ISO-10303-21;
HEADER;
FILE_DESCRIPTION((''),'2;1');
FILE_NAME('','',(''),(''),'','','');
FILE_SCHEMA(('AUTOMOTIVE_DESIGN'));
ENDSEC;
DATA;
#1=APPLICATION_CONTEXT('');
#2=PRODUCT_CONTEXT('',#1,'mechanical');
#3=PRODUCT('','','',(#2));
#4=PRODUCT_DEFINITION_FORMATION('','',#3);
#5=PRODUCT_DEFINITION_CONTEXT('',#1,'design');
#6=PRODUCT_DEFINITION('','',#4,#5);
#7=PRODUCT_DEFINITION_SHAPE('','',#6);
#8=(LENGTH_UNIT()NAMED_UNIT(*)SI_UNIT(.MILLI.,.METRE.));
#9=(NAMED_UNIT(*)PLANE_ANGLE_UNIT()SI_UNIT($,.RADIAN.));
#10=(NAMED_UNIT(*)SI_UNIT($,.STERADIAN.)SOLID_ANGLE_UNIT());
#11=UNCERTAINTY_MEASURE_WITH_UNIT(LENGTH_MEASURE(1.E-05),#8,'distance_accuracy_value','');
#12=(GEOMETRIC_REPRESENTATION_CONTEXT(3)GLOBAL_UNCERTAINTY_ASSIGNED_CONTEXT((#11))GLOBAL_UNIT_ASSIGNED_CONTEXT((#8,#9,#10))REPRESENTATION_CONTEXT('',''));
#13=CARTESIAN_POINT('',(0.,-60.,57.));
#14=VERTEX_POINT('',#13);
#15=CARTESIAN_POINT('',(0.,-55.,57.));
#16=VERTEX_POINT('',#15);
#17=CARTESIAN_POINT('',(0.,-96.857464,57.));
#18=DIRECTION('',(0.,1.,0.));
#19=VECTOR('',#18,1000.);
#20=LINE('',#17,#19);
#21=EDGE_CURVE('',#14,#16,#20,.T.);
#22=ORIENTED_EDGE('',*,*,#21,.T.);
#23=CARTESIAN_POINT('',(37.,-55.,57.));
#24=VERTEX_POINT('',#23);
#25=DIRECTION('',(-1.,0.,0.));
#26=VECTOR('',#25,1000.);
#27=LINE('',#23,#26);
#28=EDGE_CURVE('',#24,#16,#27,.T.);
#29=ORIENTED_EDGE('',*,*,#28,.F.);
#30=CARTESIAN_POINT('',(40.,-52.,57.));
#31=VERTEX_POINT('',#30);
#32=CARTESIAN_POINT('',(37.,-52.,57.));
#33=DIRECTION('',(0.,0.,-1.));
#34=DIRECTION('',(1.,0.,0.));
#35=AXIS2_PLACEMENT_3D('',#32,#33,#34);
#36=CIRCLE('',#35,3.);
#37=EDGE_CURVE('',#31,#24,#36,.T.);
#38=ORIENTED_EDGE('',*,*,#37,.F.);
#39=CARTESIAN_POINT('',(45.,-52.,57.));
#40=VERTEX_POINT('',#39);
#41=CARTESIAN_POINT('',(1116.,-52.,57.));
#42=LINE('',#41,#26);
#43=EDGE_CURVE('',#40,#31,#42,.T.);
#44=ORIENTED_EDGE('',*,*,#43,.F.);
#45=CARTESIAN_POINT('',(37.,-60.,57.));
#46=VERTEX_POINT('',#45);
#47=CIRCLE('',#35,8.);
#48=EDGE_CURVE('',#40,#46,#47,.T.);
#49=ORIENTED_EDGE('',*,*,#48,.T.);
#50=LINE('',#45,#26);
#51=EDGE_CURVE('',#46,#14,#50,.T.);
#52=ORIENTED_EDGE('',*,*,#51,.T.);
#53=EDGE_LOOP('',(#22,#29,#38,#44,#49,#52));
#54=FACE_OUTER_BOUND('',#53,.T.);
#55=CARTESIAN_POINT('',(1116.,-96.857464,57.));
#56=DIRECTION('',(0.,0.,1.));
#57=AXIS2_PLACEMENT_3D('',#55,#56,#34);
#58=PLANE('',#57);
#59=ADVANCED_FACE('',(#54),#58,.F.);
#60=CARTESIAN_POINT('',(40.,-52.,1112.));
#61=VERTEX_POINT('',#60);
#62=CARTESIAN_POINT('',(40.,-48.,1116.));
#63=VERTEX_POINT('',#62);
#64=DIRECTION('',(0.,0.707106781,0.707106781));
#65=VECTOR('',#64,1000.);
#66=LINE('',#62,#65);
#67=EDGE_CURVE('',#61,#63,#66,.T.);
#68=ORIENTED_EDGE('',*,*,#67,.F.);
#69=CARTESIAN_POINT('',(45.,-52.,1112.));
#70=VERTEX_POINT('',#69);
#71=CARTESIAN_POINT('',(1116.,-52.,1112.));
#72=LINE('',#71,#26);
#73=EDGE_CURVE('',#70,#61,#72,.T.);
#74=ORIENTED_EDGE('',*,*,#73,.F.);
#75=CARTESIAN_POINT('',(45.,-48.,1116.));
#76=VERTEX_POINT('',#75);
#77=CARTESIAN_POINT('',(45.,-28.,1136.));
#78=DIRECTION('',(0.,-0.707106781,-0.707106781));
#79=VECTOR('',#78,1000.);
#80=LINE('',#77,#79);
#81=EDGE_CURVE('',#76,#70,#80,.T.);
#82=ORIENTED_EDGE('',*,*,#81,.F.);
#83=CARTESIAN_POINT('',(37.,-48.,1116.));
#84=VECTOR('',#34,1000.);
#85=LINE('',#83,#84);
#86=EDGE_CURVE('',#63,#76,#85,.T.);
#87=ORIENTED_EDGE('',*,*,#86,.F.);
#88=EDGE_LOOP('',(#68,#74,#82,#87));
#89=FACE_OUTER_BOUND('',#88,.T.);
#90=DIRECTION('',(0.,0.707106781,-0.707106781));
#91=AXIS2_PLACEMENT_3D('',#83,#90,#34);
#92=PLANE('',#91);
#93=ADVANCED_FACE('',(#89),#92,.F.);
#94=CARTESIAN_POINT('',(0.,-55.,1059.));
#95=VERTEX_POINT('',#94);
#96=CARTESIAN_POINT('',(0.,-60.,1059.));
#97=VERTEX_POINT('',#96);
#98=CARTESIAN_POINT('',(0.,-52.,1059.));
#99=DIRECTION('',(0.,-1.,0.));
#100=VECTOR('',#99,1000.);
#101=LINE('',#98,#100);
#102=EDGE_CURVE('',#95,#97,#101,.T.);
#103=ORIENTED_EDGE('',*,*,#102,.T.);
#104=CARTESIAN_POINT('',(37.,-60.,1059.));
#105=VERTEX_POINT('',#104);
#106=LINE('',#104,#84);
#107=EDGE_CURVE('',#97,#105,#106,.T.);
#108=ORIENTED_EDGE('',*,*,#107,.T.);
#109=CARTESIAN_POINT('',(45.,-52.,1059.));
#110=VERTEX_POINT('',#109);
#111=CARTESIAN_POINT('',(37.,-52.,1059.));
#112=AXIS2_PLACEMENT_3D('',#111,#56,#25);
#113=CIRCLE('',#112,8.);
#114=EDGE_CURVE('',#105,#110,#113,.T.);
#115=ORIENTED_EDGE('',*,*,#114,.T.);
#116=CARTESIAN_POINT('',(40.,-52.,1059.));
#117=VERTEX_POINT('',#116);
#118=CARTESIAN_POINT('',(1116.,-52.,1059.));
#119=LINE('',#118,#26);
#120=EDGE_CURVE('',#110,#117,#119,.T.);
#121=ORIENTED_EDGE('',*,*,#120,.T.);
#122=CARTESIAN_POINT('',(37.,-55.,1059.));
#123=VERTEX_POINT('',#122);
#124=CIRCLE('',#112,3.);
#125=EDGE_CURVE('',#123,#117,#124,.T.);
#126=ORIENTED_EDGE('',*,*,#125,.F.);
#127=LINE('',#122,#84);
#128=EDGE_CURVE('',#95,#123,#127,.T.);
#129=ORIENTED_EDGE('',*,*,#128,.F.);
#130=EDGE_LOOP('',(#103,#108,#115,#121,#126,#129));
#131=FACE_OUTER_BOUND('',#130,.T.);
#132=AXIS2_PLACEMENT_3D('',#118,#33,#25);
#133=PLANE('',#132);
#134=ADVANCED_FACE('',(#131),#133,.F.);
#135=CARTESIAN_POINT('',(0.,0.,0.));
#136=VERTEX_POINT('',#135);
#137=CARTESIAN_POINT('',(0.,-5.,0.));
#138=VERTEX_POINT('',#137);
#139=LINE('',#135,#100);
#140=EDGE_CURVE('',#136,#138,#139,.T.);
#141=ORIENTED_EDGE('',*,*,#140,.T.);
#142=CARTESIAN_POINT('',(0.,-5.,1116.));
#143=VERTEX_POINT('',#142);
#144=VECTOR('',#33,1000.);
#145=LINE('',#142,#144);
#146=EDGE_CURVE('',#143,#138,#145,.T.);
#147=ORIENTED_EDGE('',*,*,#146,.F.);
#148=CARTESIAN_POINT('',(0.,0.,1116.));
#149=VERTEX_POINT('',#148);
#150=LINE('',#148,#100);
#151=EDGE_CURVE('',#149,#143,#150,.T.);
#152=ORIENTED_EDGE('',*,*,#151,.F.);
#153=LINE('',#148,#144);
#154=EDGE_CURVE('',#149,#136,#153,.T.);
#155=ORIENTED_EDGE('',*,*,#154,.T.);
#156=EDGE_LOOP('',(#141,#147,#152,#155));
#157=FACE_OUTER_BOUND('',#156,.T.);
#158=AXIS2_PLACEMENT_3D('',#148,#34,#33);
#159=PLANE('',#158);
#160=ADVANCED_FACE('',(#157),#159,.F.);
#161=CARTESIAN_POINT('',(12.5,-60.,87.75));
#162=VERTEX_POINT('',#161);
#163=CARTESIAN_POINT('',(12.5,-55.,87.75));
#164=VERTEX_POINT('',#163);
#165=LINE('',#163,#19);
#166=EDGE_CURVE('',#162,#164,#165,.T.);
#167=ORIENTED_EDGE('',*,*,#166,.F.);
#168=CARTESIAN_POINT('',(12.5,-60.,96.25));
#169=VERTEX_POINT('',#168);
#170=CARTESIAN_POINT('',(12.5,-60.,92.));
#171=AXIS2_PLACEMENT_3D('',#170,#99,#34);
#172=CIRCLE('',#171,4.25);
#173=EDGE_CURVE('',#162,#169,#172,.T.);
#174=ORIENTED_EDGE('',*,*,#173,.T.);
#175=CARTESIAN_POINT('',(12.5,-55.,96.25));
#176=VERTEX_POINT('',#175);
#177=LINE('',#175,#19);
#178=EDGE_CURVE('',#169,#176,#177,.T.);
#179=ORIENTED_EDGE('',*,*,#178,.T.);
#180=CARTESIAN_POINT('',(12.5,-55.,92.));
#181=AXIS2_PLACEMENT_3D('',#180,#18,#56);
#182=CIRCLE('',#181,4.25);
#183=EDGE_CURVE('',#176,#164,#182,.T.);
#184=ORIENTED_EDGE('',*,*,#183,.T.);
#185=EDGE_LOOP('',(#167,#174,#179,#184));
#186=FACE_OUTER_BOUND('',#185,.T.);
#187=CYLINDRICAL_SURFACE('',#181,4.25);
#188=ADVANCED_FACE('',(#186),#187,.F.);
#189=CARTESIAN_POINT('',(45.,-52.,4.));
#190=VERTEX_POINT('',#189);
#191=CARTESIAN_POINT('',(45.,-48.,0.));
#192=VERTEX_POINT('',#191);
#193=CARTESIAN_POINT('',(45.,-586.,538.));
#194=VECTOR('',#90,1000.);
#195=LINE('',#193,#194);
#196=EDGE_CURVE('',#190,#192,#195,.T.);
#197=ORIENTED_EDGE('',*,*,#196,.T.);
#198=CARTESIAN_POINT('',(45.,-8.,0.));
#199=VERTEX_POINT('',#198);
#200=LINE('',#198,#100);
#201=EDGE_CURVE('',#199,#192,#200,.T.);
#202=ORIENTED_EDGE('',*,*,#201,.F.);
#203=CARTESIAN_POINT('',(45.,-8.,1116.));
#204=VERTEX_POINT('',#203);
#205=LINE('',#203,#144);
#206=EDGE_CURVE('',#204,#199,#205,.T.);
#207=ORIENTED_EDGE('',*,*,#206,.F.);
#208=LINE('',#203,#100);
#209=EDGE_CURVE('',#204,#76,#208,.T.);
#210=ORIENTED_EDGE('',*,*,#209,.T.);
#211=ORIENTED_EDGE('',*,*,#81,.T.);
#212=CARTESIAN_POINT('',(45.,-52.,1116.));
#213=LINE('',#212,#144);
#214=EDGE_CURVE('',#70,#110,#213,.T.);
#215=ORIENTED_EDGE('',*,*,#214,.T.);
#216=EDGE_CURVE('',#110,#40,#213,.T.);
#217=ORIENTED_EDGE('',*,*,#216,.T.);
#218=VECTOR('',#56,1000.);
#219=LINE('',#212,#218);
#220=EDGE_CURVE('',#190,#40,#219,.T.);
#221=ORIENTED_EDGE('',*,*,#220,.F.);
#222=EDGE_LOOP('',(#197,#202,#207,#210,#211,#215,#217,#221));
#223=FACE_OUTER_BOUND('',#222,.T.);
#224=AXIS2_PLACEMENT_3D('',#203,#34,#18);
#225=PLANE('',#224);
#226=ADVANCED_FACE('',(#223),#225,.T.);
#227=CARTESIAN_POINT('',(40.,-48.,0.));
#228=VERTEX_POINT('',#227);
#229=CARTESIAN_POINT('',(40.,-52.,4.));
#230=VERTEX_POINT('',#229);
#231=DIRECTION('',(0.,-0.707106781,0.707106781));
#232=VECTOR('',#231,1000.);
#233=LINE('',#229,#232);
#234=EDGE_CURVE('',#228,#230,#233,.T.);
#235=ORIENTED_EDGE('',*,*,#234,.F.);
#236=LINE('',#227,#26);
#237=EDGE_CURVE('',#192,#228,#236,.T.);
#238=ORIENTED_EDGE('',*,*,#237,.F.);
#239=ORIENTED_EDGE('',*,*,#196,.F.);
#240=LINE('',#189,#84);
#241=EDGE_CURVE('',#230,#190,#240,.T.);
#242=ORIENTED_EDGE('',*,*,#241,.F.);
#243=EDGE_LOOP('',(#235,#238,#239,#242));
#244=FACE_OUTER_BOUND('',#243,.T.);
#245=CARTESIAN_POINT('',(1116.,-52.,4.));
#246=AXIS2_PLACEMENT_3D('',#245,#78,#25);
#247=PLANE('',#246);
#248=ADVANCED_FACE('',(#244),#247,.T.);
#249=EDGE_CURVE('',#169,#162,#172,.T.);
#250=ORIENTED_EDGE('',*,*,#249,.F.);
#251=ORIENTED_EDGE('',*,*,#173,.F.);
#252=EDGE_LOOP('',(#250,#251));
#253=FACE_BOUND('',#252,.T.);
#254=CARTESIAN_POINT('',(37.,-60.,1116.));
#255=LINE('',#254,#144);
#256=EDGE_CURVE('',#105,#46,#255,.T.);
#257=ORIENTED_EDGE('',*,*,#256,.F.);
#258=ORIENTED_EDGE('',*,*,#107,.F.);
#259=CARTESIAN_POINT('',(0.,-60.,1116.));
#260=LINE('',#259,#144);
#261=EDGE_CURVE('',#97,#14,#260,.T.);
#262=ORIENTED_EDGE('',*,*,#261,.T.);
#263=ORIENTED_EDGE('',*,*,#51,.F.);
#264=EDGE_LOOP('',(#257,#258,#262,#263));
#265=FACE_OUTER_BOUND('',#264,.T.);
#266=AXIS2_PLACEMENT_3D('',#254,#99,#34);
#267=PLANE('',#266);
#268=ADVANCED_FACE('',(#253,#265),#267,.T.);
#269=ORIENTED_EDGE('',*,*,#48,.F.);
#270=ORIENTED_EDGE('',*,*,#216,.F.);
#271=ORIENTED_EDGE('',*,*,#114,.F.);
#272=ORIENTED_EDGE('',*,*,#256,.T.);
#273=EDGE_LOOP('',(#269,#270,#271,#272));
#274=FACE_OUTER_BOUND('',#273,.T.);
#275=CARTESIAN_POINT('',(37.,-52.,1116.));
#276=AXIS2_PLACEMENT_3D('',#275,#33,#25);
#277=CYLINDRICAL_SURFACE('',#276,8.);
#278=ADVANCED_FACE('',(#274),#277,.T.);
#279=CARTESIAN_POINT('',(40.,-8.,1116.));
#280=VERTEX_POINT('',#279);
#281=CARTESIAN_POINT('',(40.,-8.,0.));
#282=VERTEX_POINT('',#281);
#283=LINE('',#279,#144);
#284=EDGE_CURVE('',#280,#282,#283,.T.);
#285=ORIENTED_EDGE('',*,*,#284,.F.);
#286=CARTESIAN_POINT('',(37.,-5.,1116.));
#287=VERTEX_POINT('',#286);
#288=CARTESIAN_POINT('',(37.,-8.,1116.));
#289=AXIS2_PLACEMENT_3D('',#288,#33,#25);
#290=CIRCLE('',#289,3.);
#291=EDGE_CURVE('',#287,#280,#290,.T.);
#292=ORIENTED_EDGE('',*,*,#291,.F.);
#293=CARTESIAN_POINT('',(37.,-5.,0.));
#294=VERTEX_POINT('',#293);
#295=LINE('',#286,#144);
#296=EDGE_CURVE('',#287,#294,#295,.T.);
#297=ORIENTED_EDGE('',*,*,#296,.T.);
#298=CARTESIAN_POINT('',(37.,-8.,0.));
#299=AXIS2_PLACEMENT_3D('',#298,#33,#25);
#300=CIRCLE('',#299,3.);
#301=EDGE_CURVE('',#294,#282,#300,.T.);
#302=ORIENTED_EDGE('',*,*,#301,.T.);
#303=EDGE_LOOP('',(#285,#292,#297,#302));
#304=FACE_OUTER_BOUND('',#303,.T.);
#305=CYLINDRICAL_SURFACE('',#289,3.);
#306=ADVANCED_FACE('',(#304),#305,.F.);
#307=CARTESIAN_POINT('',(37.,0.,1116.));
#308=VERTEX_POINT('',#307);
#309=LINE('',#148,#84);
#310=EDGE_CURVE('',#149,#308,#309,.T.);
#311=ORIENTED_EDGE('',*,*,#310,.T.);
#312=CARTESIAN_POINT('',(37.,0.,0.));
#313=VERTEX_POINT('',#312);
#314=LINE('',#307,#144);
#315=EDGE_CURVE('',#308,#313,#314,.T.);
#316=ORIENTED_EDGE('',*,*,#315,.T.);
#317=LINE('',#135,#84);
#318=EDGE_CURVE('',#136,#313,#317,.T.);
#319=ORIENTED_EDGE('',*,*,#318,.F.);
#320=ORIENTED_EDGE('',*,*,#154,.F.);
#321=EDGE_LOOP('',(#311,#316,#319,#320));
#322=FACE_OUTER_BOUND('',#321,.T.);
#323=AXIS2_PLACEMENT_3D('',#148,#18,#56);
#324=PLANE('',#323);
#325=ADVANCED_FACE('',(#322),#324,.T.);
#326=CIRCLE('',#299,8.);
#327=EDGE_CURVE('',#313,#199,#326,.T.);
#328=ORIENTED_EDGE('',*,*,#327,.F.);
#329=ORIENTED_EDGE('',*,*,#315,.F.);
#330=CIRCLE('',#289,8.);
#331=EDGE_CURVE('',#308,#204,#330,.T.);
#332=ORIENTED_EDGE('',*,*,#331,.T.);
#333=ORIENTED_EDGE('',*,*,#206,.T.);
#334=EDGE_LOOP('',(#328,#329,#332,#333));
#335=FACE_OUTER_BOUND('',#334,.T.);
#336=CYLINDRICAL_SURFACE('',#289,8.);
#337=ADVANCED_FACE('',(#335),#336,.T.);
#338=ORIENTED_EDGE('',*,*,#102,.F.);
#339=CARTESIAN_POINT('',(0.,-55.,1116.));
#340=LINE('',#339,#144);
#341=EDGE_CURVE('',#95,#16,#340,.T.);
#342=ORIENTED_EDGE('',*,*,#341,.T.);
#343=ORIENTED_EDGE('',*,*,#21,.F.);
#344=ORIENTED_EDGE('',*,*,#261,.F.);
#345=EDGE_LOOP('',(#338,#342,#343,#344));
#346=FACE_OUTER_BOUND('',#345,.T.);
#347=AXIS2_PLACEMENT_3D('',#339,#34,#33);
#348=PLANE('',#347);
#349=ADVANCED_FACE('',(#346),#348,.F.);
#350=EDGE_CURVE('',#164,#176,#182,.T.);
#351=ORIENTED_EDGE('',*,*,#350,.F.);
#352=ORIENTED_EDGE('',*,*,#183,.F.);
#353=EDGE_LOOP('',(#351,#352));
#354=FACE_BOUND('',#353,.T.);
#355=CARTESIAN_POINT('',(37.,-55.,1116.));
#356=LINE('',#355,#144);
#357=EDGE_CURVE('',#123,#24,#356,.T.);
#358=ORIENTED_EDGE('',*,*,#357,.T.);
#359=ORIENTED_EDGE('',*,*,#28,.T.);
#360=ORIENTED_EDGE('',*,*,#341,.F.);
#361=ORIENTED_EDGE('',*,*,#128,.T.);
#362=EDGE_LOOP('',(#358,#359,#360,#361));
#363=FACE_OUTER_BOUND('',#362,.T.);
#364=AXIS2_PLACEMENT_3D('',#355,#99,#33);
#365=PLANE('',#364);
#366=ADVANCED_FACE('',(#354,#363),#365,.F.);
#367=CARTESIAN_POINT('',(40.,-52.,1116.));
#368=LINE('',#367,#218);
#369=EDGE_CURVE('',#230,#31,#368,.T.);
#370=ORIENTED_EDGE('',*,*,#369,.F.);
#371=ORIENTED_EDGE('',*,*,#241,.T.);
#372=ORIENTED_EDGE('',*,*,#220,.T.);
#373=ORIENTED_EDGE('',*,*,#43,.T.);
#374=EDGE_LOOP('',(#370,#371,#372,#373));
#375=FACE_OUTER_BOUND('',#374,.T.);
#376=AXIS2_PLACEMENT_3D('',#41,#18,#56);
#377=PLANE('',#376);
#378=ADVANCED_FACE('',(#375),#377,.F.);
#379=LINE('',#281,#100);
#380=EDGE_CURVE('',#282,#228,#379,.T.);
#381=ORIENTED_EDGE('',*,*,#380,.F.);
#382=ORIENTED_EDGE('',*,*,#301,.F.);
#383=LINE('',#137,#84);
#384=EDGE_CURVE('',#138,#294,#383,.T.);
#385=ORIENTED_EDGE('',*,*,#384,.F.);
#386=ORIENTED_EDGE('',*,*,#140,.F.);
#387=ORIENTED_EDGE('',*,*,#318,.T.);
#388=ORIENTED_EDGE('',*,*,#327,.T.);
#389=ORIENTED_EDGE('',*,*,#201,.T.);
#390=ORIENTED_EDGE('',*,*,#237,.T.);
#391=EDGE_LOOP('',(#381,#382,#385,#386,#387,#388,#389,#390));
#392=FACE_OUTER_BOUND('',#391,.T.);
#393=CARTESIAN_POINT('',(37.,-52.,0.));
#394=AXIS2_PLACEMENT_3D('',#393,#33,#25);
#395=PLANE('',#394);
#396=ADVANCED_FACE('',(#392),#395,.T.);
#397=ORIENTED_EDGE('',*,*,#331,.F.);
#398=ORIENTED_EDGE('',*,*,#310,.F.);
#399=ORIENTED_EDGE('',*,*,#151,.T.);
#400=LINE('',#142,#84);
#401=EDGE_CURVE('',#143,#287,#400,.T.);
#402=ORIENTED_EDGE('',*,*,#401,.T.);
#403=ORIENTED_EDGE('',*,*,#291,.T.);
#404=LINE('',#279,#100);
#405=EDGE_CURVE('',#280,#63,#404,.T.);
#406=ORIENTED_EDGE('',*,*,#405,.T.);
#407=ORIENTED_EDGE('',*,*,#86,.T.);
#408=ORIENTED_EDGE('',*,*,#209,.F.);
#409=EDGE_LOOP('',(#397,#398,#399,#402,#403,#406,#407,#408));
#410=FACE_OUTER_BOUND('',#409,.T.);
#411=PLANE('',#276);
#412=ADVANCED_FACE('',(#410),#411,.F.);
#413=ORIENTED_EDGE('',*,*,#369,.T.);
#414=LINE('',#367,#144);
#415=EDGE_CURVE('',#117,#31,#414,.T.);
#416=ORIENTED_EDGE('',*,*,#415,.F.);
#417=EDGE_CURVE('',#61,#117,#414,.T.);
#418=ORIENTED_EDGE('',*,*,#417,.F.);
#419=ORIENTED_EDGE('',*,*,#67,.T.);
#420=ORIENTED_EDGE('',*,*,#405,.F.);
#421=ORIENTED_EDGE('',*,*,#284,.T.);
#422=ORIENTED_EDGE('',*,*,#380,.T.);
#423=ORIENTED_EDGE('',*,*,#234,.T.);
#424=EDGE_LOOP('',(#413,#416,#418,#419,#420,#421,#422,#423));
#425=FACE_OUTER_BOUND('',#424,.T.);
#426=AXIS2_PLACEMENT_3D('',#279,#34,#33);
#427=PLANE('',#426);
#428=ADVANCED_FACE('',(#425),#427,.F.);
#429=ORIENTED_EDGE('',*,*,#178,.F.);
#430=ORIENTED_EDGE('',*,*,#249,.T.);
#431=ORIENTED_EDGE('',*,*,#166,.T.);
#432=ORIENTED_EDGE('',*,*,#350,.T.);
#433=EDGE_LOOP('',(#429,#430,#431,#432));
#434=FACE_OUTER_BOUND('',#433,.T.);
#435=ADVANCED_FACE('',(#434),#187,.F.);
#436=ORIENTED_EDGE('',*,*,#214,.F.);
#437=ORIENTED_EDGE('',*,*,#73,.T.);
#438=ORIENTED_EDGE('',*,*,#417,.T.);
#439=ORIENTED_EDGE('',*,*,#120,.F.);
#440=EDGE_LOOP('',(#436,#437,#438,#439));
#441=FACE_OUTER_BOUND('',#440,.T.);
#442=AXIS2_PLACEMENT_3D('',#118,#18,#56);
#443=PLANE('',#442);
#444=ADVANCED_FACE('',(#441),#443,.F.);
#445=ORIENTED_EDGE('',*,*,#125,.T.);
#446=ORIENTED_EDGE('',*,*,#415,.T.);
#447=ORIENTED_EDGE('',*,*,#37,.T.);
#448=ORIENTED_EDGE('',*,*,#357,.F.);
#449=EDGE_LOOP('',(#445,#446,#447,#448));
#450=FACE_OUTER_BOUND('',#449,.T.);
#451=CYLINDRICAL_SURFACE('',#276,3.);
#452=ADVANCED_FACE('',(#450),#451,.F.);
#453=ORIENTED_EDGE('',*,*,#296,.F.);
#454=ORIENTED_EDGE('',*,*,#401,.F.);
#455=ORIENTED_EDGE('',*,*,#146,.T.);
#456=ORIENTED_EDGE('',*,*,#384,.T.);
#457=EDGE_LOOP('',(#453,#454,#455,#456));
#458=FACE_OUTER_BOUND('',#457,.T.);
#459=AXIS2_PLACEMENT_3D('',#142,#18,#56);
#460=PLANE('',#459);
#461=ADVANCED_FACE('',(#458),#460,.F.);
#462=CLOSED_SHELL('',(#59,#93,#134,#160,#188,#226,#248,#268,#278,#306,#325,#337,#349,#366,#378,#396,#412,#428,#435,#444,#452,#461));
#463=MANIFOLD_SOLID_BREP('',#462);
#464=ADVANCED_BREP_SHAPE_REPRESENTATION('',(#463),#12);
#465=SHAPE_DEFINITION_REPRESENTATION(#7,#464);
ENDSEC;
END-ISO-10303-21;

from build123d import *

# Parameters (mm, degrees)
BOSS_EXTRUDE1_DEPTH    = 1116
SKETCH2_W              = 92.475127077
SKETCH2_H              = 38.646657261
SKETCH2_W_2            = 90.397253408
SKETCH2_H_2            = 44.857464027
CUT_EXTRUDE1_DEPTH     = 1116
SKETCH3_R              = 4
CUT_EXTRUDE2_DEPTH     = 1116
M10_TAPPED_HOLE1_D     = 8.5
M10_TAPPED_HOLE1_DEPTH = 24.5
M10_TAPPED_HOLE1_TIP   = 2.553657631
CHAMFER1_SIZE          = 4


with BuildPart() as part:
    # Sketch1 → Boss-Extrude1 (new body)
    with BuildSketch(Plane.XY):
        with BuildLine():
            Line((0, 0), (37, 0))
            ThreePointArc((37, 0), (42.656854249, -2.343145751), (45, -8))
            Line((45, -8), (45, -52))
            ThreePointArc((45, -52), (42.656854249, -57.656854249), (37, -60))
            Line((37, -60), (0, -60))
            Line((0, -60), (0, -55))
            Line((0, -55), (37, -55))
            ThreePointArc((37, -55), (39.121320344, -54.121320344), (40, -52))
            Line((40, -52), (40, -8))
            ThreePointArc((40, -8), (39.121320344, -5.878679656), (37, -5))
            Line((37, -5), (0, -5))
            Line((0, -5), (0, 0))
        make_face()
    extrude(amount=BOSS_EXTRUDE1_DEPTH)

    # Sketch2 → Cut-Extrude1 (cut)
    with BuildSketch(Plane.ZY):
        with Locations((1105.237563539, -71.323328631)):
            Rectangle(SKETCH2_W, SKETCH2_H)
        with Locations((11.801373296, -74.428732013)):
            Rectangle(SKETCH2_W_2, SKETCH2_H_2)
    extrude(amount=-CUT_EXTRUDE1_DEPTH, mode=Mode.SUBTRACT)

    # Sketch3 → Cut-Extrude2 (cut)
    with BuildSketch(Plane(origin=(0, -55, 0), x_dir=(1, 0, 0), z_dir=(0, 1, 0))):
        with Locations(Location((12.5, -92, 0), (0, 0, 270))):
            Circle(SKETCH3_R)
    extrude(amount=-CUT_EXTRUDE2_DEPTH, mode=Mode.SUBTRACT)

    # M10 Tapped Hole1
    with Locations(Plane(origin=(0, -55, 0), x_dir=(1, 0, 0), z_dir=(0, 1, 0))):
        with Locations((12.5, -92)):
            Hole(M10_TAPPED_HOLE1_D / 2, depth=M10_TAPPED_HOLE1_DEPTH)
            with Locations((0, 0, -(M10_TAPPED_HOLE1_DEPTH + M10_TAPPED_HOLE1_TIP / 2))):  # 118° drill point
                Cone(0, M10_TAPPED_HOLE1_D / 2, M10_TAPPED_HOLE1_TIP, mode=Mode.SUBTRACT)

    # Chamfer1
    chamfer1_edges = [part.edges().sort_by_distance(p)[0] for p in [
        (42.5, -52, 0),
        (42.5, -52, 1116),
    ]]
    chamfer(chamfer1_edges, length=CHAMFER1_SIZE)


solid = part.part
